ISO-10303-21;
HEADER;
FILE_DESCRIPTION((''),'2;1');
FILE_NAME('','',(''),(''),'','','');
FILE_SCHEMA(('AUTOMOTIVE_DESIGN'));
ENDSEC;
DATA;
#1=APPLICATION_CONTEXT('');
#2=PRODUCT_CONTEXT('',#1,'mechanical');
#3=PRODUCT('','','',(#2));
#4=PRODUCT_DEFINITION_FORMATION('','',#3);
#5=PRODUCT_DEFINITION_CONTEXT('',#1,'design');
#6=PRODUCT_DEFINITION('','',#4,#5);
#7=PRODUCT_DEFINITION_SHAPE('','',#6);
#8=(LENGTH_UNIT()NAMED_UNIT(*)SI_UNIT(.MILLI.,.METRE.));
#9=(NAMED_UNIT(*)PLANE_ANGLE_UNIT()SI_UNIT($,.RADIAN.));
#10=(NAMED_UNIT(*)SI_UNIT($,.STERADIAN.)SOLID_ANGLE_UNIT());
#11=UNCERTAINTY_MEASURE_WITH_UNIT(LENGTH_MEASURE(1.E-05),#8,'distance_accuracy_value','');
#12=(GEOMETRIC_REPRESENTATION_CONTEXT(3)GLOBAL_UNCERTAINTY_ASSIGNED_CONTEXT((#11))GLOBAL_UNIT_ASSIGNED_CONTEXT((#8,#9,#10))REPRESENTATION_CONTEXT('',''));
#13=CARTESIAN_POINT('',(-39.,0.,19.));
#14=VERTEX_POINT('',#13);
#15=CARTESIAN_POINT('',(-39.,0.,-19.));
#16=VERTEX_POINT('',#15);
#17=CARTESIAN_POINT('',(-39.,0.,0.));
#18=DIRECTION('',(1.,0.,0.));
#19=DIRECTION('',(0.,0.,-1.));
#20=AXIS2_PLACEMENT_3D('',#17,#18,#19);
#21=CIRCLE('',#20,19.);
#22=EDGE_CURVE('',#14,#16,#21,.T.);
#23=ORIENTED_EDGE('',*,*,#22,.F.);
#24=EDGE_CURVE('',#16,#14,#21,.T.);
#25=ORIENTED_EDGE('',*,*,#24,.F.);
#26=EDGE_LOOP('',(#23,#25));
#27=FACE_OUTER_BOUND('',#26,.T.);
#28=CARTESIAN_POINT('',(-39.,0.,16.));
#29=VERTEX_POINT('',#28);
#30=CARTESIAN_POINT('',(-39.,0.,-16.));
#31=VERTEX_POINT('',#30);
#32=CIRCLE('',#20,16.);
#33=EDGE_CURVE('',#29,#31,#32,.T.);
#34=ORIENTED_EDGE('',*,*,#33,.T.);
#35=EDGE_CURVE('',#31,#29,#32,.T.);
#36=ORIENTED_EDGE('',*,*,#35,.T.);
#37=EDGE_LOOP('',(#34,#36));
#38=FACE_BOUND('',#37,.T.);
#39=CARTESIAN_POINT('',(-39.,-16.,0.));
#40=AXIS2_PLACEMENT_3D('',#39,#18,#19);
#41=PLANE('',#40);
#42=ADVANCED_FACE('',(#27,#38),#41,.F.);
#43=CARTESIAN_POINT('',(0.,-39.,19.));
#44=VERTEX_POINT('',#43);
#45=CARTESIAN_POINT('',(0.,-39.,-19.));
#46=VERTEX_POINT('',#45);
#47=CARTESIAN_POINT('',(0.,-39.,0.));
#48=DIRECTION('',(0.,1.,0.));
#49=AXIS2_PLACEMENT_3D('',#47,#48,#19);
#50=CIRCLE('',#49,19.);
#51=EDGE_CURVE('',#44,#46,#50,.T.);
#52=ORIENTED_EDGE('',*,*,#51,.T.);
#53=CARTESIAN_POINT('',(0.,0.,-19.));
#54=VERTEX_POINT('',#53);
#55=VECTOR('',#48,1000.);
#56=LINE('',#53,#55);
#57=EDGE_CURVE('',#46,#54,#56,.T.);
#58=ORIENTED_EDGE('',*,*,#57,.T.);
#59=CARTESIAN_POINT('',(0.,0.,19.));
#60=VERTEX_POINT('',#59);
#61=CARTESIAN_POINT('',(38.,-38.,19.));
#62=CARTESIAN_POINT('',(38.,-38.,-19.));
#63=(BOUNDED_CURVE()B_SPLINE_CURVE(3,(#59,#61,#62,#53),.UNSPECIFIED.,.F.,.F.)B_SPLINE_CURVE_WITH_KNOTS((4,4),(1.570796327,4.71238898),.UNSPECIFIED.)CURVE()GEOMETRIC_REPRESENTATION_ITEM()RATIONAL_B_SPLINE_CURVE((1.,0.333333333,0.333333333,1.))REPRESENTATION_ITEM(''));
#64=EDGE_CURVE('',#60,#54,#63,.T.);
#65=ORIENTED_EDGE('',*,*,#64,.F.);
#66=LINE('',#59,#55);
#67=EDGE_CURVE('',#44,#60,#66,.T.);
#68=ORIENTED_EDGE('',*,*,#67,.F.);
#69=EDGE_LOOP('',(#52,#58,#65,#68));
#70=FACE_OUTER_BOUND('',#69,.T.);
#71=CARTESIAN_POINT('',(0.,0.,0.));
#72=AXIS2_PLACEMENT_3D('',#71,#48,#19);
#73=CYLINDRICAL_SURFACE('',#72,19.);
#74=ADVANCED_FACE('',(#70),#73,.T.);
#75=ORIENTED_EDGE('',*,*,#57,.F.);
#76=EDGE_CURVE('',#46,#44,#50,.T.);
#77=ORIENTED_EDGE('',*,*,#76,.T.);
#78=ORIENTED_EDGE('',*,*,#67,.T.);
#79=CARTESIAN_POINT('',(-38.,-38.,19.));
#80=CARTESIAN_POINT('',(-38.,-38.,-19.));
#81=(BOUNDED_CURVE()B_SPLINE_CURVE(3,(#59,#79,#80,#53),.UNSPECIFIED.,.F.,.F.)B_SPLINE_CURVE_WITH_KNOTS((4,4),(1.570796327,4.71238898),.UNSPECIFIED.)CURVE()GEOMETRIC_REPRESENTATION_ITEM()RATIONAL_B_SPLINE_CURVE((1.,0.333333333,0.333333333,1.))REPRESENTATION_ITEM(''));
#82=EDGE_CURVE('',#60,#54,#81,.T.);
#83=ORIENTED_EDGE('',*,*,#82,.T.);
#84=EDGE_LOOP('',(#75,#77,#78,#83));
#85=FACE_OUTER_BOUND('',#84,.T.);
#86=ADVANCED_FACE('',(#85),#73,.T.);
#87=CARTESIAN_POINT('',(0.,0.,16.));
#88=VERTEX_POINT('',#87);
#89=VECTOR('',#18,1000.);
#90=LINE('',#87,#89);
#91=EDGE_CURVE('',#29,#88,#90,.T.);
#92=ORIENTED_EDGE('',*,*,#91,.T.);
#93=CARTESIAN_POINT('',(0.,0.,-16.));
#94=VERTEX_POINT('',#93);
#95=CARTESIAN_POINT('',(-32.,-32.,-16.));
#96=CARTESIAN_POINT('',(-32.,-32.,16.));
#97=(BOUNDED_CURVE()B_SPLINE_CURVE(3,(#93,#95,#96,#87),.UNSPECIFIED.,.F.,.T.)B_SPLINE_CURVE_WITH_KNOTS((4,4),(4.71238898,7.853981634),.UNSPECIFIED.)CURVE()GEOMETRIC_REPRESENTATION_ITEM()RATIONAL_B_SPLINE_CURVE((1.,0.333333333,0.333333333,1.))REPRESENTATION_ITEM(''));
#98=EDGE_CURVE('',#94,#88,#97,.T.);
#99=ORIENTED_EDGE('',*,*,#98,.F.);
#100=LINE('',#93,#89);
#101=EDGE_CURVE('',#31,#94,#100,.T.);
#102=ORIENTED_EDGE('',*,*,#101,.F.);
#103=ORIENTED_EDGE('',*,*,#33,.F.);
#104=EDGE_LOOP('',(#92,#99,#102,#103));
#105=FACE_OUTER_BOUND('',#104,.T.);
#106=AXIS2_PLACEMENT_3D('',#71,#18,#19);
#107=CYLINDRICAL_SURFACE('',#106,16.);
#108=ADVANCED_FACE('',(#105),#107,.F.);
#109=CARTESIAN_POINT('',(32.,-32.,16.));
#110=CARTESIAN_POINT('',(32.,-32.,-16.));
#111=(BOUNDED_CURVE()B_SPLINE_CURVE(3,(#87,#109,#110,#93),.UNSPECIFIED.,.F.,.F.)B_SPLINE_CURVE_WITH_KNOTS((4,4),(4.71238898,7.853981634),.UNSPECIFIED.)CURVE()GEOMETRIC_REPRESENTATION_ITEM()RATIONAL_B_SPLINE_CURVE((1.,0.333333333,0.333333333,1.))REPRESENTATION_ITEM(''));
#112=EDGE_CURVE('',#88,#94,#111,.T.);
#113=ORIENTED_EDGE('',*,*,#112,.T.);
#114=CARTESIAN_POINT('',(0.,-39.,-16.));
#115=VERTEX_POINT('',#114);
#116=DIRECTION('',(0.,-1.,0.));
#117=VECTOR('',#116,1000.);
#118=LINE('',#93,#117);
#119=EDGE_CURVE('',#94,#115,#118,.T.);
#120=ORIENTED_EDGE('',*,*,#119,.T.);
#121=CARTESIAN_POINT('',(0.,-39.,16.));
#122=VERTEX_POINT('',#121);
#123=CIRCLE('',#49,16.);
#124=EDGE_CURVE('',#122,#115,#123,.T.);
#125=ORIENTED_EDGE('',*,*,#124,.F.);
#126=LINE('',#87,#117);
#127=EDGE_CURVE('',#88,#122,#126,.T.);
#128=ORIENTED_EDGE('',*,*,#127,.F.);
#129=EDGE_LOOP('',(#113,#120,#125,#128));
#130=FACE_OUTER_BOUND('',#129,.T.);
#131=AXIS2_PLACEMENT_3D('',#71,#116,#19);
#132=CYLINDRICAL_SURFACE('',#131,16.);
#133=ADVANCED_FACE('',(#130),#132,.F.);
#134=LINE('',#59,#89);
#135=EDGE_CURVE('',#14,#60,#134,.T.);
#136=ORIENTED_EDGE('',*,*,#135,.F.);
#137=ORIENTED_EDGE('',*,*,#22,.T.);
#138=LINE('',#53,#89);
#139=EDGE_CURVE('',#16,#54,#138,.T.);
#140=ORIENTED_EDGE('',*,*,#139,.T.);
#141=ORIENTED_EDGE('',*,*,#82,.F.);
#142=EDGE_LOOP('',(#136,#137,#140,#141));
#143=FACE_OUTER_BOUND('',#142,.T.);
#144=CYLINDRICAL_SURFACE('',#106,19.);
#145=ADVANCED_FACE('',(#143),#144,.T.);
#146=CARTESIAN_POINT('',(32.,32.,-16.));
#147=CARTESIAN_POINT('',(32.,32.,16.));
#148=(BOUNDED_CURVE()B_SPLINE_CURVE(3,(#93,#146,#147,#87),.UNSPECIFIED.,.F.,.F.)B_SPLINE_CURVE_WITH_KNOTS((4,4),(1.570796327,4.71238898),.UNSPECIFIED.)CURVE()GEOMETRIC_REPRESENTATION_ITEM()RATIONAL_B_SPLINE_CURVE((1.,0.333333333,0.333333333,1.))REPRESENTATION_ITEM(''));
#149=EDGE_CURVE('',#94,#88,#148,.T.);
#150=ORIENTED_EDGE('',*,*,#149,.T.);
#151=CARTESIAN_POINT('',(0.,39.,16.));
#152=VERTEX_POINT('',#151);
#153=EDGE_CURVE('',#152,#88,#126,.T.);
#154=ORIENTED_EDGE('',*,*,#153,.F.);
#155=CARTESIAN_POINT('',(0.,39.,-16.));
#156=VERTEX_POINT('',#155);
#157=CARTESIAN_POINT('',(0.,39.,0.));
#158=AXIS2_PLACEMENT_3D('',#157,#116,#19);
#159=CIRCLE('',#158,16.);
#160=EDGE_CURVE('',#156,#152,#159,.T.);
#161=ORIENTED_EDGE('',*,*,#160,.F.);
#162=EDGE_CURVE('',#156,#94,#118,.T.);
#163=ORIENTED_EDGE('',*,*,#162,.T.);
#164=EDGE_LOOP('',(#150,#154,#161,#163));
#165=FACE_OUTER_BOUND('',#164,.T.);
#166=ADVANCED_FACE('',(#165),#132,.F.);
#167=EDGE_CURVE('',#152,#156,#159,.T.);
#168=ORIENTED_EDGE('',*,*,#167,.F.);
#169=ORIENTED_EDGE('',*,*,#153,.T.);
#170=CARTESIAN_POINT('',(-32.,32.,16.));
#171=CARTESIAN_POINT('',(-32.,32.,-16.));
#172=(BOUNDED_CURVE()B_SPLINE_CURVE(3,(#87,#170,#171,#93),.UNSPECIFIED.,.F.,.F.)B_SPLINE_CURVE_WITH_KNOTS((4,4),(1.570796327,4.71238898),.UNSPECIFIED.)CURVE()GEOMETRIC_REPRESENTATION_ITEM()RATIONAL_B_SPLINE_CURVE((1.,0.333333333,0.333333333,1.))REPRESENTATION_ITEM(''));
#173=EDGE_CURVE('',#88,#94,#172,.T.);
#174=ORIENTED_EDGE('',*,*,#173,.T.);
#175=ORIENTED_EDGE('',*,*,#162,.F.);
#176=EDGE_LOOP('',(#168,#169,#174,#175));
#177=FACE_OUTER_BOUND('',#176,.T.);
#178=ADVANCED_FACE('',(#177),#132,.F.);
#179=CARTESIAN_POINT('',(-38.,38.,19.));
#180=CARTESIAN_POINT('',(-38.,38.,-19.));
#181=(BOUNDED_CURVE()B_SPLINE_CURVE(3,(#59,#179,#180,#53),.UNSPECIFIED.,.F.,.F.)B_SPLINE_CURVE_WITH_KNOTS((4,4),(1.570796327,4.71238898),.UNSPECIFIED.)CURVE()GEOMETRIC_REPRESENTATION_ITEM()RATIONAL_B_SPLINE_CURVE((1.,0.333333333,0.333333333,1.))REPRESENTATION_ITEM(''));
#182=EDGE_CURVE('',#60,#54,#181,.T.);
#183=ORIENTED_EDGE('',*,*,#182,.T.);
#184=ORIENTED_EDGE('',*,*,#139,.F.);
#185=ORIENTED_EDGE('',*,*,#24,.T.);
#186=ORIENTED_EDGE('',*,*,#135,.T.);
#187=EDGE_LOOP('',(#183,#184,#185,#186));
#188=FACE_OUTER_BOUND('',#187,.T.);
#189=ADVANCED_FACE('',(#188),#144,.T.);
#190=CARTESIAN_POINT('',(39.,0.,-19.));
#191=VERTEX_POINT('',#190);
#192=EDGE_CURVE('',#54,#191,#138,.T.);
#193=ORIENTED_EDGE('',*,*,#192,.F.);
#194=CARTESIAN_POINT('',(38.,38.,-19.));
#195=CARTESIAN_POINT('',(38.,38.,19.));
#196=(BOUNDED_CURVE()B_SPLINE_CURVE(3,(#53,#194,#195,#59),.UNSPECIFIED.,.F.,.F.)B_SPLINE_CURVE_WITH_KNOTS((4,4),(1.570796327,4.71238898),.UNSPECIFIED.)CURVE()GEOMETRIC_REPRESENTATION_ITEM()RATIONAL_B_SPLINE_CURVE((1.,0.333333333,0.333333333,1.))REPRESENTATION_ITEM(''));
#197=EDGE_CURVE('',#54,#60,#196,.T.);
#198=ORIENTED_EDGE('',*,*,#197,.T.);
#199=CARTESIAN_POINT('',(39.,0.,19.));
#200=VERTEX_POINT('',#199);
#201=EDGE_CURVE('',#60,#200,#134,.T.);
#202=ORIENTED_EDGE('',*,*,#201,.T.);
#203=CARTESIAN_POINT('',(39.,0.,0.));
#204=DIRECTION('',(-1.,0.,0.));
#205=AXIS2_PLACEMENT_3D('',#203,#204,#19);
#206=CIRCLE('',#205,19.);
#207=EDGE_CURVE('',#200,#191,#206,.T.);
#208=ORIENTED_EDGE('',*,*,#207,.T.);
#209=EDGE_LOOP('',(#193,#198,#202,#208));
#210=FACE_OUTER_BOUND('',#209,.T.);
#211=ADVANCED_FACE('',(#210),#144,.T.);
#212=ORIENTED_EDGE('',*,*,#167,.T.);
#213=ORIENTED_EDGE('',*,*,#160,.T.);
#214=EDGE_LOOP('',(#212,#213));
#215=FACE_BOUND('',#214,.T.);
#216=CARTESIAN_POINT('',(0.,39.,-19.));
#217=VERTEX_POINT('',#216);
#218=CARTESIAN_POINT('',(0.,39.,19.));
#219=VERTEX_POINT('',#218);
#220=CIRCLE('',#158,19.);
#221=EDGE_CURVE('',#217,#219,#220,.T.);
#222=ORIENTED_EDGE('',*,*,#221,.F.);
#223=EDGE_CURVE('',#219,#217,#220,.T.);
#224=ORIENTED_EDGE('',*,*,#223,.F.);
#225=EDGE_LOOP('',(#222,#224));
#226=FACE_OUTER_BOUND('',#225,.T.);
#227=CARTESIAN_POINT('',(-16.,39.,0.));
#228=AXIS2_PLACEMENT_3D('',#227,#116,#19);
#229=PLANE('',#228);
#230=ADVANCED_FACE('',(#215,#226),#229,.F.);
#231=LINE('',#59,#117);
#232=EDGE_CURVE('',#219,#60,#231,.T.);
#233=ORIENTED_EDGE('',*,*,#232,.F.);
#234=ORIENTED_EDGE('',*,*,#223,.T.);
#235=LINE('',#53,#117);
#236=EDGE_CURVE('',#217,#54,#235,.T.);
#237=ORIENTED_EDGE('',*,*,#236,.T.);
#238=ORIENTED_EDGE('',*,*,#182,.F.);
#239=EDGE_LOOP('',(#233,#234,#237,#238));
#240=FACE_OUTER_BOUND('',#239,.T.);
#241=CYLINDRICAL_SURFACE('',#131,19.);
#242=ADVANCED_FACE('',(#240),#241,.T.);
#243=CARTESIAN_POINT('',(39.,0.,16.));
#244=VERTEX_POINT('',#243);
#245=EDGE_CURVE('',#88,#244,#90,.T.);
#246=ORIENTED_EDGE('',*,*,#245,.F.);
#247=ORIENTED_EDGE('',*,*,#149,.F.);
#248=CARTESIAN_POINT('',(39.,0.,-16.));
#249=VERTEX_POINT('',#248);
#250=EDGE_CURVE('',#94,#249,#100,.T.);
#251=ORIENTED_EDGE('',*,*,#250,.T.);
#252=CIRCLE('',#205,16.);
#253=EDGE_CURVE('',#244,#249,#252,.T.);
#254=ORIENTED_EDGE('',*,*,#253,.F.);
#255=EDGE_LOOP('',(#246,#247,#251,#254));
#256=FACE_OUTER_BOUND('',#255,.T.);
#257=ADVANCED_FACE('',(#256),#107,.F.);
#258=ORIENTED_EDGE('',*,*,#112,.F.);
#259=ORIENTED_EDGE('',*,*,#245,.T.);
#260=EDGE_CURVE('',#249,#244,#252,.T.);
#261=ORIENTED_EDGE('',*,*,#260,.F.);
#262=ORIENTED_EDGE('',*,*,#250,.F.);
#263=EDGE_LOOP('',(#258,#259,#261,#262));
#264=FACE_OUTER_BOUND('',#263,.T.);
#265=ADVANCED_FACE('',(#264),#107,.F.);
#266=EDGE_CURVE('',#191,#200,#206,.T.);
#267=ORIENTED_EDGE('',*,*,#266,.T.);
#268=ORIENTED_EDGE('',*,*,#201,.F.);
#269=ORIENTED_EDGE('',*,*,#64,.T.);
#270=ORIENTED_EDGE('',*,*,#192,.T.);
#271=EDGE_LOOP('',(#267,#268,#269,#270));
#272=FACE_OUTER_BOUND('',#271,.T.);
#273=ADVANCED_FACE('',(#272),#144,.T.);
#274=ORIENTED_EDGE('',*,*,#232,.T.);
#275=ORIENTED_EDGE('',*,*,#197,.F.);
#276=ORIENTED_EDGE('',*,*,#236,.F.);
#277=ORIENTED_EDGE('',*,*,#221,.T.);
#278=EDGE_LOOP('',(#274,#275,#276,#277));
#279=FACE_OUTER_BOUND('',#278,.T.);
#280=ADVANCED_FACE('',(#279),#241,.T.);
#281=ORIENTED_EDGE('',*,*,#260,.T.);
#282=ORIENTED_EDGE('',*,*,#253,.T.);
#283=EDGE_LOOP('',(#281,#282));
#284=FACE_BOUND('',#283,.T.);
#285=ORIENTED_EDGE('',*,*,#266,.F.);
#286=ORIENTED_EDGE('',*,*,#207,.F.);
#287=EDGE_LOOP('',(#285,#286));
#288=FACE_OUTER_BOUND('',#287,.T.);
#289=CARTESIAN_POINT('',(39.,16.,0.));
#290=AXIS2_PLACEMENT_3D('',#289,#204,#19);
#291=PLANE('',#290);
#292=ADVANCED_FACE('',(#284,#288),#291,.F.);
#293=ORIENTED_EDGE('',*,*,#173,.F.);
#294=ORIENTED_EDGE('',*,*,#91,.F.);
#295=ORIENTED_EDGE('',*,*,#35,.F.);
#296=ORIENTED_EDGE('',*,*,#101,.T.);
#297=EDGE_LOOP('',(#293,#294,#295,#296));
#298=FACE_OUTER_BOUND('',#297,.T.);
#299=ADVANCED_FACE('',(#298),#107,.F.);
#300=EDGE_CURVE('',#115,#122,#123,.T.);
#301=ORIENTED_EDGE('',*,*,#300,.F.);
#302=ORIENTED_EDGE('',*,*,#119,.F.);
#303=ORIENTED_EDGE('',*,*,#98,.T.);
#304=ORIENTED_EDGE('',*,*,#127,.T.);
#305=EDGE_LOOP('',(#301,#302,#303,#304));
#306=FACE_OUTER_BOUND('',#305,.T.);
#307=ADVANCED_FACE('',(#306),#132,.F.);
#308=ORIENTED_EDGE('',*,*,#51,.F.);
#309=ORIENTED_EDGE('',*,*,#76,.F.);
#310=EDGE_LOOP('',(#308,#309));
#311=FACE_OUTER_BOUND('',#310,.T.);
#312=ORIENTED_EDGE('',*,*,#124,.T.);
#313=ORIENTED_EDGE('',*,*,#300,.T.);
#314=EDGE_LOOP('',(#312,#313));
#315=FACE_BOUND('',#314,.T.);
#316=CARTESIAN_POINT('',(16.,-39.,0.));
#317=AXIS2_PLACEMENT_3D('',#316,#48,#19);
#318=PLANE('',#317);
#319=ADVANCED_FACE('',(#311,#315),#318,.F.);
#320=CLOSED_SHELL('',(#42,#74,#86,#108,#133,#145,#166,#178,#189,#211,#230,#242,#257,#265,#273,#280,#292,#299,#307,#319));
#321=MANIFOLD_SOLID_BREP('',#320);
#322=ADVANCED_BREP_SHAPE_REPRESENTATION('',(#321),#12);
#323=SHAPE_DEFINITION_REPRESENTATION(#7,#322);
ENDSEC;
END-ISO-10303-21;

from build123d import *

# Parameters (mm, degrees)
SKETCH_1_W               = 3
SKETCH_1_H               = 39
PATTERN_CIRCULAR_1_COUNT = 4
SKETCH_5_R               = 16
CUT_EXTRUDE_1_DEPTH      = 90.252451078
SKETCH_6_R               = 16
CUT_EXTRUDE_2_DEPTH      = 90.252451078


with BuildPart() as part:
    # 草图1 → 旋转1 (revolve)
    with BuildSketch(Plane.XY, mode=Mode.PRIVATE) as revolve_1_sk:
        with Locations((-17.5, 19.5)):
            Rectangle(SKETCH_1_W, SKETCH_1_H)
    revolve_1 = revolve(revolve_1_sk.sketch.rotate(Axis((0, 0, 0), (0, 1, 0)), 270), axis=Axis((0, 0, 0), (0, 1, 0)))

    # 阵列(圆周)1: 旋转1 ×4 about axis
    pattern_circular_1_axis = Axis((0, 0, 0), (0, 0, 1))
    for i in range(1, PATTERN_CIRCULAR_1_COUNT):
        add(revolve_1.rotate(pattern_circular_1_axis, i * 360 / PATTERN_CIRCULAR_1_COUNT))

    # 草图5 → 切除-拉伸1 (cut, through all)
    with BuildSketch(Plane(origin=(0, 39, 0), x_dir=(1, 0, 0), z_dir=(0, 1, 0))):
        with Locations(Location((0, 0, 0), (0, 0, 90))):
            Circle(SKETCH_5_R)
    extrude(amount=-CUT_EXTRUDE_1_DEPTH, mode=Mode.SUBTRACT)

    # 草图6 → 切除-拉伸2 (cut, through all)
    with BuildSketch(Plane(origin=(39, 0, 0), x_dir=(0, 0, -1), z_dir=(1, 0, 0))):
        Circle(SKETCH_6_R)
    extrude(amount=-CUT_EXTRUDE_2_DEPTH, mode=Mode.SUBTRACT)


solid = part.part
